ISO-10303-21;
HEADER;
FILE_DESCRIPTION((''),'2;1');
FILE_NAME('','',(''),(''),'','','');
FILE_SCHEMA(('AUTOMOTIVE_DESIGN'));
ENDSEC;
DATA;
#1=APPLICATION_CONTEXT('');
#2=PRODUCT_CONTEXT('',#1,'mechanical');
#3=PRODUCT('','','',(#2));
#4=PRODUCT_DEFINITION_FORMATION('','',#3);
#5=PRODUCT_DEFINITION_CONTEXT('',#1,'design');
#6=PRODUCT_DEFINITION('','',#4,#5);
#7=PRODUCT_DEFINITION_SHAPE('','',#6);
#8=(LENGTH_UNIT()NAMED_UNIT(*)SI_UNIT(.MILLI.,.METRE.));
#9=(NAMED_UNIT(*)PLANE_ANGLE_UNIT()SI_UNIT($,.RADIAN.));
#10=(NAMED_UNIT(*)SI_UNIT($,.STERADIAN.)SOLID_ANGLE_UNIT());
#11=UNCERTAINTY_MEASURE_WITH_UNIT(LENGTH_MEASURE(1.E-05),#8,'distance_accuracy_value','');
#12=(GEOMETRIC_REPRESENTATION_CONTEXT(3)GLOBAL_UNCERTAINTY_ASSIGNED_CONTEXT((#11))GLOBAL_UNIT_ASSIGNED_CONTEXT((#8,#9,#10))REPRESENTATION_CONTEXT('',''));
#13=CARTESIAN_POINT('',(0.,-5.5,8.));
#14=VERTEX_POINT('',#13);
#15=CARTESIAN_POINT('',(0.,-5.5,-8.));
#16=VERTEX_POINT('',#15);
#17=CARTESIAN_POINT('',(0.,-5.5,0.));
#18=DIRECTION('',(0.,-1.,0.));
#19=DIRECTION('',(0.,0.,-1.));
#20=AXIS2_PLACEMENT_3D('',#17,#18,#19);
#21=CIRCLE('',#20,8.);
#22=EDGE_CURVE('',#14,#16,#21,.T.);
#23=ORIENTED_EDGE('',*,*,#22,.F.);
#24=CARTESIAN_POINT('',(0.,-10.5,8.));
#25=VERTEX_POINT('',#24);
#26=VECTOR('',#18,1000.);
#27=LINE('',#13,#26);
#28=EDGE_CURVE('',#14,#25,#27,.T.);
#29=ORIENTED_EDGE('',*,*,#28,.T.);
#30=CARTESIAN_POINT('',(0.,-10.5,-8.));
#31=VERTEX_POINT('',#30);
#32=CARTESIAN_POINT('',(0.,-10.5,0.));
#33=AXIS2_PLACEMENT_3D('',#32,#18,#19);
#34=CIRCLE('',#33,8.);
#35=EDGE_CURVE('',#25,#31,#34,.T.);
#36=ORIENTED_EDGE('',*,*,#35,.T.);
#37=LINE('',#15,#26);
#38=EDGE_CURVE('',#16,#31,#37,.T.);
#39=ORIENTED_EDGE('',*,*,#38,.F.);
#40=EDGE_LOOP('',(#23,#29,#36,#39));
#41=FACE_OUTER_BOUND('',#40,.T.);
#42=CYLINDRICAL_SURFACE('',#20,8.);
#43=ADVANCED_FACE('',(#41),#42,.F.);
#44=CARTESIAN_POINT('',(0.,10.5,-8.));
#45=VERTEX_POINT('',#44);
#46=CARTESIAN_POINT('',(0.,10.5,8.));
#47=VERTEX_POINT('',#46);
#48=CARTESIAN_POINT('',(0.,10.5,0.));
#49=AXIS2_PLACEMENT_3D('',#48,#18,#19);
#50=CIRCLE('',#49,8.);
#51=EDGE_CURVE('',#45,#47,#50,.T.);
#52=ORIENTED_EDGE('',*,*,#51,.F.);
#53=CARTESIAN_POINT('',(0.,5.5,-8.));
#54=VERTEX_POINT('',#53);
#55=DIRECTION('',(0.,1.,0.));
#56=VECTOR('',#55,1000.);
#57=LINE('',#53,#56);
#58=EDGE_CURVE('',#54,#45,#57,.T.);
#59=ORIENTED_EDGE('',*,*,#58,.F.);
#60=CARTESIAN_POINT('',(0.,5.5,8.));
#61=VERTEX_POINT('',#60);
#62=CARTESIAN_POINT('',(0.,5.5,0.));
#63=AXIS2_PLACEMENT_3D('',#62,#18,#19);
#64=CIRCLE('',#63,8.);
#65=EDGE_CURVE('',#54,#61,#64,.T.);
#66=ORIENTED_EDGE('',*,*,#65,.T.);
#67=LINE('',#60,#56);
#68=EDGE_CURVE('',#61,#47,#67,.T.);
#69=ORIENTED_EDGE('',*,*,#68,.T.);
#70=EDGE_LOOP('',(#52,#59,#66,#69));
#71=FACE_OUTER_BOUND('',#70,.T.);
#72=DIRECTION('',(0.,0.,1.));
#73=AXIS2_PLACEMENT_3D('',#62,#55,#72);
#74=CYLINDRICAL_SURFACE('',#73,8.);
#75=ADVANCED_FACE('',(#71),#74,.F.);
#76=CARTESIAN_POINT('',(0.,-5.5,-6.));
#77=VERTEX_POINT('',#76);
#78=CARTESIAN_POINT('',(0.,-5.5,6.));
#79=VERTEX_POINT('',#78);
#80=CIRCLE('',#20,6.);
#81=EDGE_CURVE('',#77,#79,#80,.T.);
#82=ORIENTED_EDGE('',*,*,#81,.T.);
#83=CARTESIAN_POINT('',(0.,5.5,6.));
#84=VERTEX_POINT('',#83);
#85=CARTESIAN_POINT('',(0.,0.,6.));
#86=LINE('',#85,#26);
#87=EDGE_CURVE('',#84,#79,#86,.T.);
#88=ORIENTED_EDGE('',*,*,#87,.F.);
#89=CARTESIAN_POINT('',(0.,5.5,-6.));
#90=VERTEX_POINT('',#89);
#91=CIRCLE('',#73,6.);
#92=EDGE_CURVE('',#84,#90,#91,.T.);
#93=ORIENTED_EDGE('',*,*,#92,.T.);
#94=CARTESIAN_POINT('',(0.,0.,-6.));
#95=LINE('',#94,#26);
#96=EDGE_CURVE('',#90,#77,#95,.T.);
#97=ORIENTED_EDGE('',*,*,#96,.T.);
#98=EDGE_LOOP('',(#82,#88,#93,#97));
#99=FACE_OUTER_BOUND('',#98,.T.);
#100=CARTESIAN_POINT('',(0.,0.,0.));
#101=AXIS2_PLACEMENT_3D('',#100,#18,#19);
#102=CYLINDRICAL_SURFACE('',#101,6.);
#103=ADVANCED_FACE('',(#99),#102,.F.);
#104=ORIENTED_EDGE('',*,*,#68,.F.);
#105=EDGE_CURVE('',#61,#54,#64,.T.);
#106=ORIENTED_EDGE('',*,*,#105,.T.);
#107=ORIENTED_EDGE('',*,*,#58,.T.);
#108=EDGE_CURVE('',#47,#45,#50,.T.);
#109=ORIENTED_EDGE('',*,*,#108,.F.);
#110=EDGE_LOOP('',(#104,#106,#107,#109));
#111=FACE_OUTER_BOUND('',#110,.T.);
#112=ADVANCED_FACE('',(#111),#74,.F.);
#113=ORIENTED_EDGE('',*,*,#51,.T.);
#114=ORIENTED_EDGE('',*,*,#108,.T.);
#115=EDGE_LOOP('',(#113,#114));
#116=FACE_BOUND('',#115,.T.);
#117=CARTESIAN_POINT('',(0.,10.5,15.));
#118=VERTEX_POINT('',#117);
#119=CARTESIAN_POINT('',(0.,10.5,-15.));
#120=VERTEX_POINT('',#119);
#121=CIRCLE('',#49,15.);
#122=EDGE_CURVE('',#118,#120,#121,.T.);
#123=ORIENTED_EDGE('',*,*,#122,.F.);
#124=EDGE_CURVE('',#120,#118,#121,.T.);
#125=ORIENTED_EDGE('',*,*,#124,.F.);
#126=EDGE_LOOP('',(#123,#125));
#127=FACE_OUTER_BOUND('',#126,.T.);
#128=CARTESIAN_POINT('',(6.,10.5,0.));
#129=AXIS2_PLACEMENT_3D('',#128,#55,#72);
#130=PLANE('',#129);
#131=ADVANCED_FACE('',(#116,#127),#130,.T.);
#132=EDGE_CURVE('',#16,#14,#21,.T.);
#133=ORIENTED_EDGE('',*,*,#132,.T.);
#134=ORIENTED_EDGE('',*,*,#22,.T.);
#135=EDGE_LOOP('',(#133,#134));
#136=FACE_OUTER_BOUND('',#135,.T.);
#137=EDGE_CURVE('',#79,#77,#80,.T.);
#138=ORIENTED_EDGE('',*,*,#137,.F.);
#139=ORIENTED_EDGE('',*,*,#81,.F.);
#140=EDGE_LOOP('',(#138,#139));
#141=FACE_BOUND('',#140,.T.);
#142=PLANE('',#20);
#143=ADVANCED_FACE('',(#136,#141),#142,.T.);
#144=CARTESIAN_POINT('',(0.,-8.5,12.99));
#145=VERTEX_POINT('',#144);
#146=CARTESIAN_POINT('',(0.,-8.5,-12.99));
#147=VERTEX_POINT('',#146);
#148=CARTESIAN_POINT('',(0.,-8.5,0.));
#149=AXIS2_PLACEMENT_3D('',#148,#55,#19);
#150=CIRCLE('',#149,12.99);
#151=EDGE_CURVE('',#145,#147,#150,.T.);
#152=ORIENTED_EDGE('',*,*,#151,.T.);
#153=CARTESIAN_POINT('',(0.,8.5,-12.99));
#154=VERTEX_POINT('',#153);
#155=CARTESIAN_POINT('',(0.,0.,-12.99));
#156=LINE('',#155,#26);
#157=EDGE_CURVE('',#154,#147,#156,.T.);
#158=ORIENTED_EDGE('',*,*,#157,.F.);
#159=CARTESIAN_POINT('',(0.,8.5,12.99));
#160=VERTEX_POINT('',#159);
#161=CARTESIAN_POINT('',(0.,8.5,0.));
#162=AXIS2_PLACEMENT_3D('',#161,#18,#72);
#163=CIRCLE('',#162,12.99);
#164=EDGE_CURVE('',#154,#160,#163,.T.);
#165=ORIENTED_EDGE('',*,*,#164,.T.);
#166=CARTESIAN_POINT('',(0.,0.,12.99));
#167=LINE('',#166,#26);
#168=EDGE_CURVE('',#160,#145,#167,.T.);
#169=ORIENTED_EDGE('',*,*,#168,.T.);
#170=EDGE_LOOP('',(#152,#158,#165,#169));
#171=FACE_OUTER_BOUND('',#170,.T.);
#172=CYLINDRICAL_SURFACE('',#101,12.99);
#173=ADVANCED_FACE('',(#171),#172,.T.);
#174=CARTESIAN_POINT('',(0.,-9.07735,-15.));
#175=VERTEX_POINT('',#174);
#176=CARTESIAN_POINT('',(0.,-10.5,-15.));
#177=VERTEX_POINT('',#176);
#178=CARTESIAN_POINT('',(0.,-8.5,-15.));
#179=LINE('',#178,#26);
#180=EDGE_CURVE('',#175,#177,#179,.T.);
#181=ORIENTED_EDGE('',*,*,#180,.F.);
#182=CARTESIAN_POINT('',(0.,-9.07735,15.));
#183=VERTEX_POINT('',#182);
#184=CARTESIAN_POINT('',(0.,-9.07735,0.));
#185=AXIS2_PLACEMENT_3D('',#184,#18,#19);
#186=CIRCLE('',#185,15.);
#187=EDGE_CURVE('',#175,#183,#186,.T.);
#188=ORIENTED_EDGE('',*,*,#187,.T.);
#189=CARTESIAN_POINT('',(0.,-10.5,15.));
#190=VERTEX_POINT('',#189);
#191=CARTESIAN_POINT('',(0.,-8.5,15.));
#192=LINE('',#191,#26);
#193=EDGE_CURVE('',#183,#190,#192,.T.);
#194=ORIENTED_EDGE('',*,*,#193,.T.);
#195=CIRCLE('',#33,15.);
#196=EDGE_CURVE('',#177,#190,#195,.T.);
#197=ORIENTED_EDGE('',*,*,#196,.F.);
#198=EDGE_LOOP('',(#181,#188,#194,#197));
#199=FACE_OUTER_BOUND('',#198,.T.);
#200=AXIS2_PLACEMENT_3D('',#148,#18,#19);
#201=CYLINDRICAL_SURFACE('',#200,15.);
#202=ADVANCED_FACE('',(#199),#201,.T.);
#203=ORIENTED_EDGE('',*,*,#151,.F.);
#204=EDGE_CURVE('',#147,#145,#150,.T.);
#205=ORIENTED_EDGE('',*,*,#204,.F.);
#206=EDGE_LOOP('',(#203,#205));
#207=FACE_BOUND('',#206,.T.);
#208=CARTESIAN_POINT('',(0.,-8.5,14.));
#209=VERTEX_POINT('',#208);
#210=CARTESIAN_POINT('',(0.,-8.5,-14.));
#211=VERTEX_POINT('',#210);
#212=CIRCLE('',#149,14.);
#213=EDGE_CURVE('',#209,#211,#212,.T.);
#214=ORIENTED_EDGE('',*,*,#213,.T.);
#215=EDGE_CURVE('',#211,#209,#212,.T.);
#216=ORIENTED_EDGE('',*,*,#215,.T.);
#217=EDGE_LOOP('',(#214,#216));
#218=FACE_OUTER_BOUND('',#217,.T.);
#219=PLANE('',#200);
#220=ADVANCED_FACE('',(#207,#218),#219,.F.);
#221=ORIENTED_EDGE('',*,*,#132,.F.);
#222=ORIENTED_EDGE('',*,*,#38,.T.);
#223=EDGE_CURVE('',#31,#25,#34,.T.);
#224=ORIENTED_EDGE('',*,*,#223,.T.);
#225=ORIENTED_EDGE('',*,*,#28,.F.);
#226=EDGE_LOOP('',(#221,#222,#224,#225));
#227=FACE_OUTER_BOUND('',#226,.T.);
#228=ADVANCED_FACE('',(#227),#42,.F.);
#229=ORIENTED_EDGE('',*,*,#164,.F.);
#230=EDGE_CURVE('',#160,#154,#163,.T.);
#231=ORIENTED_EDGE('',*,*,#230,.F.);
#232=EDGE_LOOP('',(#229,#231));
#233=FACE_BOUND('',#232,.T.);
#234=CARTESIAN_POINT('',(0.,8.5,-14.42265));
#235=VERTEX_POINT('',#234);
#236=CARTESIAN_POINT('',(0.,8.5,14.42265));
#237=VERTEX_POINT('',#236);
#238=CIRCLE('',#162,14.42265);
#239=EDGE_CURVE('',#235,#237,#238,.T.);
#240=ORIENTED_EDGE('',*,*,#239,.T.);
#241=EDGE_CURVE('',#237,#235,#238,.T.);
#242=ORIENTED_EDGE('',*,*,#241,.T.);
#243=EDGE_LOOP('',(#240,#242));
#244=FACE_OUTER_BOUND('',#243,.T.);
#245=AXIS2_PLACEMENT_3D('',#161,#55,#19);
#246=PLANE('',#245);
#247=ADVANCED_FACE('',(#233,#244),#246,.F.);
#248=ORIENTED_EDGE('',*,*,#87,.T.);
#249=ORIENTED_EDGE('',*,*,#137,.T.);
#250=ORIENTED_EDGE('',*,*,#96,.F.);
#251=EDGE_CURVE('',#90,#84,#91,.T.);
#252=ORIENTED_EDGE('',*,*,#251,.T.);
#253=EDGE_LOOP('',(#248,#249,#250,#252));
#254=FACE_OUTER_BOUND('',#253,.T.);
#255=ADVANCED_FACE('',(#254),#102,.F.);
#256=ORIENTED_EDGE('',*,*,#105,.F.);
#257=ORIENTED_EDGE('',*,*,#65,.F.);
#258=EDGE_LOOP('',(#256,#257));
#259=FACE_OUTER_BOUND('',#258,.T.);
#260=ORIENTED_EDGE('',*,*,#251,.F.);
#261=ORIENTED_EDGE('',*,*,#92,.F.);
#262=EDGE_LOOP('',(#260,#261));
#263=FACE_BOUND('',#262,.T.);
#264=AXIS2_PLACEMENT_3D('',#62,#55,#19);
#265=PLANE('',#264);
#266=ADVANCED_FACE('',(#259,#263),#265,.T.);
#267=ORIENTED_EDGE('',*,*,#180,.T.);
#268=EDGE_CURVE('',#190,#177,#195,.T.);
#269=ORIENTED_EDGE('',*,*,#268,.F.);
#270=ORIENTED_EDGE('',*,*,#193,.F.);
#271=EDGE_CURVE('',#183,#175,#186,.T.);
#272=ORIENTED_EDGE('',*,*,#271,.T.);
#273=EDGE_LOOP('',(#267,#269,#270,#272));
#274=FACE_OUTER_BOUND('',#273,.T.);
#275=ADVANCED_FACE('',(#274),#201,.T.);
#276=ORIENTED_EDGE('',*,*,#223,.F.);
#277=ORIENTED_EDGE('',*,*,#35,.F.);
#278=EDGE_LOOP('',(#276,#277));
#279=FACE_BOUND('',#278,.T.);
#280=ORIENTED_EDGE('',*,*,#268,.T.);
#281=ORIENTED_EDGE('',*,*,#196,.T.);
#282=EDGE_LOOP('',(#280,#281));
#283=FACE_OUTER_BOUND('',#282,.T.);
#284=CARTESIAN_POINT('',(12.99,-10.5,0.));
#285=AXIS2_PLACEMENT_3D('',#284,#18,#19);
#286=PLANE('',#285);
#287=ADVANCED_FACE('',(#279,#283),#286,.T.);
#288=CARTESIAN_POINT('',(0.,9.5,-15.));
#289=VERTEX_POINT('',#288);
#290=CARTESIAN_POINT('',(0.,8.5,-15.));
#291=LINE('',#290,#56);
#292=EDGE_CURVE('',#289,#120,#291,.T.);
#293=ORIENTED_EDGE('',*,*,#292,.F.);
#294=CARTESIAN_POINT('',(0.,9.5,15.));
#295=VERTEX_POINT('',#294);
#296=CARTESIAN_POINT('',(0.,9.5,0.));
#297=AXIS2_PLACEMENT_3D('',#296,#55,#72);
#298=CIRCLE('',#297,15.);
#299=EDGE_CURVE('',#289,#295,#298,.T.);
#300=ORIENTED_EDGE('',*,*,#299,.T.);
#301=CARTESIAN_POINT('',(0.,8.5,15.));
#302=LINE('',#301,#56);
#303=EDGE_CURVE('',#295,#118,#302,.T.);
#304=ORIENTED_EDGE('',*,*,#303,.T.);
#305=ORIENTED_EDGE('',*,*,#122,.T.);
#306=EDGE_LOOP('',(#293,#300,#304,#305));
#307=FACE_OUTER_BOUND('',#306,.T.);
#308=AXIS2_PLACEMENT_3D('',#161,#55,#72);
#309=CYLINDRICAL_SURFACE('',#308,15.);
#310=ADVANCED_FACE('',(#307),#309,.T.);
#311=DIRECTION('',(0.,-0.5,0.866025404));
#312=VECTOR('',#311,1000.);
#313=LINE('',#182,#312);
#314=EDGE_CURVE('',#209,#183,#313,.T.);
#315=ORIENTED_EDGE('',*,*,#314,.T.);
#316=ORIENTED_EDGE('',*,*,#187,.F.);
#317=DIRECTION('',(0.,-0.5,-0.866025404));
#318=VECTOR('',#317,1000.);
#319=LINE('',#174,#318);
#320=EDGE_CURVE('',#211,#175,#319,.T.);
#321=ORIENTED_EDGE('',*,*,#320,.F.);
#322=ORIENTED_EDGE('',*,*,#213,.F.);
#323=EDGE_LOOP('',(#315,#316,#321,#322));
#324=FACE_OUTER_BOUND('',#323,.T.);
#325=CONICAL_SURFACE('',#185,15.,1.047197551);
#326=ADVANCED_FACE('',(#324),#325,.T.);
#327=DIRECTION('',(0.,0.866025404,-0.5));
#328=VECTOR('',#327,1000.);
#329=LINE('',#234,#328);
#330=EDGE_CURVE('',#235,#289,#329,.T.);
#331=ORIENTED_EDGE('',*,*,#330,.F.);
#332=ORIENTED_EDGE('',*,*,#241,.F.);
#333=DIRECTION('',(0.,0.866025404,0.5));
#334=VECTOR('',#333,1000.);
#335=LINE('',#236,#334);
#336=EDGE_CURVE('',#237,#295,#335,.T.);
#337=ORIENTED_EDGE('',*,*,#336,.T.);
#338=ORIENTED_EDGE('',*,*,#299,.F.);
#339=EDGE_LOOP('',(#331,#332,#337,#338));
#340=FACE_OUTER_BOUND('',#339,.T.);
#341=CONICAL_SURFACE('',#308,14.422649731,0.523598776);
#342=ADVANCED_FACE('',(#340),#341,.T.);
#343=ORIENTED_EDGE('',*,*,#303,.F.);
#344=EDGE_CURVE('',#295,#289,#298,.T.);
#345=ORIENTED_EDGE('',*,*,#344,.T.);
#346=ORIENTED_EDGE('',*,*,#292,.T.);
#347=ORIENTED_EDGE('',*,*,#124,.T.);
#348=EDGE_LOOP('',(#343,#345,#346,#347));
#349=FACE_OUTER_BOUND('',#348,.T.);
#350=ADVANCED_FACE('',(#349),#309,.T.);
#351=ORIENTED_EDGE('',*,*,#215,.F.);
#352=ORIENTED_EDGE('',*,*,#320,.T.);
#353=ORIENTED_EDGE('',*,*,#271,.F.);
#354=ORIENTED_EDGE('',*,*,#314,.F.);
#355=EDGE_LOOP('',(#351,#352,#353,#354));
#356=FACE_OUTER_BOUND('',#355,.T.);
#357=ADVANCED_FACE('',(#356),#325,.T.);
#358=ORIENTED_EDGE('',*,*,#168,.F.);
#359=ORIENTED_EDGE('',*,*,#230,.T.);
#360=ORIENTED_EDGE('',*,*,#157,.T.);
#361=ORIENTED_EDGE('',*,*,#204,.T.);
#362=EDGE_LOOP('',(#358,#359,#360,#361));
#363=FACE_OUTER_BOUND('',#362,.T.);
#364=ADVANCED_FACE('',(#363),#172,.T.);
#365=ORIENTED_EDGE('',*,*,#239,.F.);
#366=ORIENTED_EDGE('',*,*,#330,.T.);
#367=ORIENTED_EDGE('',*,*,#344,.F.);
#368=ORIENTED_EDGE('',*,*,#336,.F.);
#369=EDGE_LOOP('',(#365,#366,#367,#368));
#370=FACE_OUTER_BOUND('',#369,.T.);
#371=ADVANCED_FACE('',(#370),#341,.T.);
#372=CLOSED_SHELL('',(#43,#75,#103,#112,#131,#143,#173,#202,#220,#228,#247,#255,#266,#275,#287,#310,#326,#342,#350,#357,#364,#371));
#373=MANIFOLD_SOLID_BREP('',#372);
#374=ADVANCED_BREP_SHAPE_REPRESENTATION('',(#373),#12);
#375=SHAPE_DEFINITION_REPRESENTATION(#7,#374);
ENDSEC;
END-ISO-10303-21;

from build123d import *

# Parameters (mm, degrees)
SKETCH_1_W          = 6.99
SKETCH_1_H          = 21
SKETCH_4_R          = 8
CUT_EXTRUDE_3_DEPTH = 5
SKETCH_5_R          = 15
SKETCH_5_R_2        = 8
EXTRUDE_1_DEPTH     = 2
CHAMFER_1_SIZE      = 1
CHAMFER_1_SIZE2     = 0.577350269
CHAMFER_2_SIZE      = 1
CHAMFER_2_SIZE2     = 0.577350269


with BuildPart() as part:
    # 草图1 → 旋转1 (revolve)
    with BuildSketch(Plane.XY, mode=Mode.PRIVATE) as revolve_1_sk:
        with Locations((9.495, 0)):
            Rectangle(SKETCH_1_W, SKETCH_1_H)
    revolve(revolve_1_sk.sketch.rotate(Axis((0, 0, 0), (0, 1, 0)), 90), axis=Axis((0, 0, 0), (0, 1, 0)))

    # 草图4 → 切除-拉伸3 (cut)
    with BuildSketch(Plane.XZ.offset(10.5)):
        with Locations(Location((0, 0, 0), (0, 0, 270))):
            Circle(SKETCH_4_R)
    cut_extrude_3 = extrude(amount=-CUT_EXTRUDE_3_DEPTH, mode=Mode.SUBTRACT)

    # 草图5 → 凸台-拉伸1 (add)
    with BuildSketch(Plane.XZ.offset(10.5)):
        with Locations(Location((0, 0, 0), (0, 0, 270))):
            Circle(SKETCH_5_R)
        with Locations(Location((0, 0, 0), (0, 0, 270))):
            Circle(SKETCH_5_R_2, mode=Mode.SUBTRACT)
    extrude_1 = extrude(amount=-EXTRUDE_1_DEPTH)

    # 镜向1: 切除-拉伸3, 凸台-拉伸1 across plane
    add(cut_extrude_3.mirror(Plane.ZX), mode=Mode.SUBTRACT)
    add(extrude_1.mirror(Plane.ZX))

    # 倒角1
    chamfer_1_edges = [part.edges().sort_by_distance(p)[0] for p in [
        (0, 8.5, 15),
    ]]
    chamfer_1_side = [part.faces().sort_by_distance(p)[0] for p in [
        (0, 9.5, 15),
    ]]
    chamfer(chamfer_1_edges, length=CHAMFER_1_SIZE, length2=CHAMFER_1_SIZE2, reference=chamfer_1_side[0])

    # 倒角2
    chamfer_2_edges = [part.edges().sort_by_distance(p)[0] for p in [
        (0, -8.5, 15),
    ]]
    chamfer_2_side = [part.faces().sort_by_distance(p)[0] for p in [
        (0, -8.5, 14.575735931),
    ]]
    chamfer(chamfer_2_edges, length=CHAMFER_2_SIZE, length2=CHAMFER_2_SIZE2, reference=chamfer_2_side[0])


solid = part.part
